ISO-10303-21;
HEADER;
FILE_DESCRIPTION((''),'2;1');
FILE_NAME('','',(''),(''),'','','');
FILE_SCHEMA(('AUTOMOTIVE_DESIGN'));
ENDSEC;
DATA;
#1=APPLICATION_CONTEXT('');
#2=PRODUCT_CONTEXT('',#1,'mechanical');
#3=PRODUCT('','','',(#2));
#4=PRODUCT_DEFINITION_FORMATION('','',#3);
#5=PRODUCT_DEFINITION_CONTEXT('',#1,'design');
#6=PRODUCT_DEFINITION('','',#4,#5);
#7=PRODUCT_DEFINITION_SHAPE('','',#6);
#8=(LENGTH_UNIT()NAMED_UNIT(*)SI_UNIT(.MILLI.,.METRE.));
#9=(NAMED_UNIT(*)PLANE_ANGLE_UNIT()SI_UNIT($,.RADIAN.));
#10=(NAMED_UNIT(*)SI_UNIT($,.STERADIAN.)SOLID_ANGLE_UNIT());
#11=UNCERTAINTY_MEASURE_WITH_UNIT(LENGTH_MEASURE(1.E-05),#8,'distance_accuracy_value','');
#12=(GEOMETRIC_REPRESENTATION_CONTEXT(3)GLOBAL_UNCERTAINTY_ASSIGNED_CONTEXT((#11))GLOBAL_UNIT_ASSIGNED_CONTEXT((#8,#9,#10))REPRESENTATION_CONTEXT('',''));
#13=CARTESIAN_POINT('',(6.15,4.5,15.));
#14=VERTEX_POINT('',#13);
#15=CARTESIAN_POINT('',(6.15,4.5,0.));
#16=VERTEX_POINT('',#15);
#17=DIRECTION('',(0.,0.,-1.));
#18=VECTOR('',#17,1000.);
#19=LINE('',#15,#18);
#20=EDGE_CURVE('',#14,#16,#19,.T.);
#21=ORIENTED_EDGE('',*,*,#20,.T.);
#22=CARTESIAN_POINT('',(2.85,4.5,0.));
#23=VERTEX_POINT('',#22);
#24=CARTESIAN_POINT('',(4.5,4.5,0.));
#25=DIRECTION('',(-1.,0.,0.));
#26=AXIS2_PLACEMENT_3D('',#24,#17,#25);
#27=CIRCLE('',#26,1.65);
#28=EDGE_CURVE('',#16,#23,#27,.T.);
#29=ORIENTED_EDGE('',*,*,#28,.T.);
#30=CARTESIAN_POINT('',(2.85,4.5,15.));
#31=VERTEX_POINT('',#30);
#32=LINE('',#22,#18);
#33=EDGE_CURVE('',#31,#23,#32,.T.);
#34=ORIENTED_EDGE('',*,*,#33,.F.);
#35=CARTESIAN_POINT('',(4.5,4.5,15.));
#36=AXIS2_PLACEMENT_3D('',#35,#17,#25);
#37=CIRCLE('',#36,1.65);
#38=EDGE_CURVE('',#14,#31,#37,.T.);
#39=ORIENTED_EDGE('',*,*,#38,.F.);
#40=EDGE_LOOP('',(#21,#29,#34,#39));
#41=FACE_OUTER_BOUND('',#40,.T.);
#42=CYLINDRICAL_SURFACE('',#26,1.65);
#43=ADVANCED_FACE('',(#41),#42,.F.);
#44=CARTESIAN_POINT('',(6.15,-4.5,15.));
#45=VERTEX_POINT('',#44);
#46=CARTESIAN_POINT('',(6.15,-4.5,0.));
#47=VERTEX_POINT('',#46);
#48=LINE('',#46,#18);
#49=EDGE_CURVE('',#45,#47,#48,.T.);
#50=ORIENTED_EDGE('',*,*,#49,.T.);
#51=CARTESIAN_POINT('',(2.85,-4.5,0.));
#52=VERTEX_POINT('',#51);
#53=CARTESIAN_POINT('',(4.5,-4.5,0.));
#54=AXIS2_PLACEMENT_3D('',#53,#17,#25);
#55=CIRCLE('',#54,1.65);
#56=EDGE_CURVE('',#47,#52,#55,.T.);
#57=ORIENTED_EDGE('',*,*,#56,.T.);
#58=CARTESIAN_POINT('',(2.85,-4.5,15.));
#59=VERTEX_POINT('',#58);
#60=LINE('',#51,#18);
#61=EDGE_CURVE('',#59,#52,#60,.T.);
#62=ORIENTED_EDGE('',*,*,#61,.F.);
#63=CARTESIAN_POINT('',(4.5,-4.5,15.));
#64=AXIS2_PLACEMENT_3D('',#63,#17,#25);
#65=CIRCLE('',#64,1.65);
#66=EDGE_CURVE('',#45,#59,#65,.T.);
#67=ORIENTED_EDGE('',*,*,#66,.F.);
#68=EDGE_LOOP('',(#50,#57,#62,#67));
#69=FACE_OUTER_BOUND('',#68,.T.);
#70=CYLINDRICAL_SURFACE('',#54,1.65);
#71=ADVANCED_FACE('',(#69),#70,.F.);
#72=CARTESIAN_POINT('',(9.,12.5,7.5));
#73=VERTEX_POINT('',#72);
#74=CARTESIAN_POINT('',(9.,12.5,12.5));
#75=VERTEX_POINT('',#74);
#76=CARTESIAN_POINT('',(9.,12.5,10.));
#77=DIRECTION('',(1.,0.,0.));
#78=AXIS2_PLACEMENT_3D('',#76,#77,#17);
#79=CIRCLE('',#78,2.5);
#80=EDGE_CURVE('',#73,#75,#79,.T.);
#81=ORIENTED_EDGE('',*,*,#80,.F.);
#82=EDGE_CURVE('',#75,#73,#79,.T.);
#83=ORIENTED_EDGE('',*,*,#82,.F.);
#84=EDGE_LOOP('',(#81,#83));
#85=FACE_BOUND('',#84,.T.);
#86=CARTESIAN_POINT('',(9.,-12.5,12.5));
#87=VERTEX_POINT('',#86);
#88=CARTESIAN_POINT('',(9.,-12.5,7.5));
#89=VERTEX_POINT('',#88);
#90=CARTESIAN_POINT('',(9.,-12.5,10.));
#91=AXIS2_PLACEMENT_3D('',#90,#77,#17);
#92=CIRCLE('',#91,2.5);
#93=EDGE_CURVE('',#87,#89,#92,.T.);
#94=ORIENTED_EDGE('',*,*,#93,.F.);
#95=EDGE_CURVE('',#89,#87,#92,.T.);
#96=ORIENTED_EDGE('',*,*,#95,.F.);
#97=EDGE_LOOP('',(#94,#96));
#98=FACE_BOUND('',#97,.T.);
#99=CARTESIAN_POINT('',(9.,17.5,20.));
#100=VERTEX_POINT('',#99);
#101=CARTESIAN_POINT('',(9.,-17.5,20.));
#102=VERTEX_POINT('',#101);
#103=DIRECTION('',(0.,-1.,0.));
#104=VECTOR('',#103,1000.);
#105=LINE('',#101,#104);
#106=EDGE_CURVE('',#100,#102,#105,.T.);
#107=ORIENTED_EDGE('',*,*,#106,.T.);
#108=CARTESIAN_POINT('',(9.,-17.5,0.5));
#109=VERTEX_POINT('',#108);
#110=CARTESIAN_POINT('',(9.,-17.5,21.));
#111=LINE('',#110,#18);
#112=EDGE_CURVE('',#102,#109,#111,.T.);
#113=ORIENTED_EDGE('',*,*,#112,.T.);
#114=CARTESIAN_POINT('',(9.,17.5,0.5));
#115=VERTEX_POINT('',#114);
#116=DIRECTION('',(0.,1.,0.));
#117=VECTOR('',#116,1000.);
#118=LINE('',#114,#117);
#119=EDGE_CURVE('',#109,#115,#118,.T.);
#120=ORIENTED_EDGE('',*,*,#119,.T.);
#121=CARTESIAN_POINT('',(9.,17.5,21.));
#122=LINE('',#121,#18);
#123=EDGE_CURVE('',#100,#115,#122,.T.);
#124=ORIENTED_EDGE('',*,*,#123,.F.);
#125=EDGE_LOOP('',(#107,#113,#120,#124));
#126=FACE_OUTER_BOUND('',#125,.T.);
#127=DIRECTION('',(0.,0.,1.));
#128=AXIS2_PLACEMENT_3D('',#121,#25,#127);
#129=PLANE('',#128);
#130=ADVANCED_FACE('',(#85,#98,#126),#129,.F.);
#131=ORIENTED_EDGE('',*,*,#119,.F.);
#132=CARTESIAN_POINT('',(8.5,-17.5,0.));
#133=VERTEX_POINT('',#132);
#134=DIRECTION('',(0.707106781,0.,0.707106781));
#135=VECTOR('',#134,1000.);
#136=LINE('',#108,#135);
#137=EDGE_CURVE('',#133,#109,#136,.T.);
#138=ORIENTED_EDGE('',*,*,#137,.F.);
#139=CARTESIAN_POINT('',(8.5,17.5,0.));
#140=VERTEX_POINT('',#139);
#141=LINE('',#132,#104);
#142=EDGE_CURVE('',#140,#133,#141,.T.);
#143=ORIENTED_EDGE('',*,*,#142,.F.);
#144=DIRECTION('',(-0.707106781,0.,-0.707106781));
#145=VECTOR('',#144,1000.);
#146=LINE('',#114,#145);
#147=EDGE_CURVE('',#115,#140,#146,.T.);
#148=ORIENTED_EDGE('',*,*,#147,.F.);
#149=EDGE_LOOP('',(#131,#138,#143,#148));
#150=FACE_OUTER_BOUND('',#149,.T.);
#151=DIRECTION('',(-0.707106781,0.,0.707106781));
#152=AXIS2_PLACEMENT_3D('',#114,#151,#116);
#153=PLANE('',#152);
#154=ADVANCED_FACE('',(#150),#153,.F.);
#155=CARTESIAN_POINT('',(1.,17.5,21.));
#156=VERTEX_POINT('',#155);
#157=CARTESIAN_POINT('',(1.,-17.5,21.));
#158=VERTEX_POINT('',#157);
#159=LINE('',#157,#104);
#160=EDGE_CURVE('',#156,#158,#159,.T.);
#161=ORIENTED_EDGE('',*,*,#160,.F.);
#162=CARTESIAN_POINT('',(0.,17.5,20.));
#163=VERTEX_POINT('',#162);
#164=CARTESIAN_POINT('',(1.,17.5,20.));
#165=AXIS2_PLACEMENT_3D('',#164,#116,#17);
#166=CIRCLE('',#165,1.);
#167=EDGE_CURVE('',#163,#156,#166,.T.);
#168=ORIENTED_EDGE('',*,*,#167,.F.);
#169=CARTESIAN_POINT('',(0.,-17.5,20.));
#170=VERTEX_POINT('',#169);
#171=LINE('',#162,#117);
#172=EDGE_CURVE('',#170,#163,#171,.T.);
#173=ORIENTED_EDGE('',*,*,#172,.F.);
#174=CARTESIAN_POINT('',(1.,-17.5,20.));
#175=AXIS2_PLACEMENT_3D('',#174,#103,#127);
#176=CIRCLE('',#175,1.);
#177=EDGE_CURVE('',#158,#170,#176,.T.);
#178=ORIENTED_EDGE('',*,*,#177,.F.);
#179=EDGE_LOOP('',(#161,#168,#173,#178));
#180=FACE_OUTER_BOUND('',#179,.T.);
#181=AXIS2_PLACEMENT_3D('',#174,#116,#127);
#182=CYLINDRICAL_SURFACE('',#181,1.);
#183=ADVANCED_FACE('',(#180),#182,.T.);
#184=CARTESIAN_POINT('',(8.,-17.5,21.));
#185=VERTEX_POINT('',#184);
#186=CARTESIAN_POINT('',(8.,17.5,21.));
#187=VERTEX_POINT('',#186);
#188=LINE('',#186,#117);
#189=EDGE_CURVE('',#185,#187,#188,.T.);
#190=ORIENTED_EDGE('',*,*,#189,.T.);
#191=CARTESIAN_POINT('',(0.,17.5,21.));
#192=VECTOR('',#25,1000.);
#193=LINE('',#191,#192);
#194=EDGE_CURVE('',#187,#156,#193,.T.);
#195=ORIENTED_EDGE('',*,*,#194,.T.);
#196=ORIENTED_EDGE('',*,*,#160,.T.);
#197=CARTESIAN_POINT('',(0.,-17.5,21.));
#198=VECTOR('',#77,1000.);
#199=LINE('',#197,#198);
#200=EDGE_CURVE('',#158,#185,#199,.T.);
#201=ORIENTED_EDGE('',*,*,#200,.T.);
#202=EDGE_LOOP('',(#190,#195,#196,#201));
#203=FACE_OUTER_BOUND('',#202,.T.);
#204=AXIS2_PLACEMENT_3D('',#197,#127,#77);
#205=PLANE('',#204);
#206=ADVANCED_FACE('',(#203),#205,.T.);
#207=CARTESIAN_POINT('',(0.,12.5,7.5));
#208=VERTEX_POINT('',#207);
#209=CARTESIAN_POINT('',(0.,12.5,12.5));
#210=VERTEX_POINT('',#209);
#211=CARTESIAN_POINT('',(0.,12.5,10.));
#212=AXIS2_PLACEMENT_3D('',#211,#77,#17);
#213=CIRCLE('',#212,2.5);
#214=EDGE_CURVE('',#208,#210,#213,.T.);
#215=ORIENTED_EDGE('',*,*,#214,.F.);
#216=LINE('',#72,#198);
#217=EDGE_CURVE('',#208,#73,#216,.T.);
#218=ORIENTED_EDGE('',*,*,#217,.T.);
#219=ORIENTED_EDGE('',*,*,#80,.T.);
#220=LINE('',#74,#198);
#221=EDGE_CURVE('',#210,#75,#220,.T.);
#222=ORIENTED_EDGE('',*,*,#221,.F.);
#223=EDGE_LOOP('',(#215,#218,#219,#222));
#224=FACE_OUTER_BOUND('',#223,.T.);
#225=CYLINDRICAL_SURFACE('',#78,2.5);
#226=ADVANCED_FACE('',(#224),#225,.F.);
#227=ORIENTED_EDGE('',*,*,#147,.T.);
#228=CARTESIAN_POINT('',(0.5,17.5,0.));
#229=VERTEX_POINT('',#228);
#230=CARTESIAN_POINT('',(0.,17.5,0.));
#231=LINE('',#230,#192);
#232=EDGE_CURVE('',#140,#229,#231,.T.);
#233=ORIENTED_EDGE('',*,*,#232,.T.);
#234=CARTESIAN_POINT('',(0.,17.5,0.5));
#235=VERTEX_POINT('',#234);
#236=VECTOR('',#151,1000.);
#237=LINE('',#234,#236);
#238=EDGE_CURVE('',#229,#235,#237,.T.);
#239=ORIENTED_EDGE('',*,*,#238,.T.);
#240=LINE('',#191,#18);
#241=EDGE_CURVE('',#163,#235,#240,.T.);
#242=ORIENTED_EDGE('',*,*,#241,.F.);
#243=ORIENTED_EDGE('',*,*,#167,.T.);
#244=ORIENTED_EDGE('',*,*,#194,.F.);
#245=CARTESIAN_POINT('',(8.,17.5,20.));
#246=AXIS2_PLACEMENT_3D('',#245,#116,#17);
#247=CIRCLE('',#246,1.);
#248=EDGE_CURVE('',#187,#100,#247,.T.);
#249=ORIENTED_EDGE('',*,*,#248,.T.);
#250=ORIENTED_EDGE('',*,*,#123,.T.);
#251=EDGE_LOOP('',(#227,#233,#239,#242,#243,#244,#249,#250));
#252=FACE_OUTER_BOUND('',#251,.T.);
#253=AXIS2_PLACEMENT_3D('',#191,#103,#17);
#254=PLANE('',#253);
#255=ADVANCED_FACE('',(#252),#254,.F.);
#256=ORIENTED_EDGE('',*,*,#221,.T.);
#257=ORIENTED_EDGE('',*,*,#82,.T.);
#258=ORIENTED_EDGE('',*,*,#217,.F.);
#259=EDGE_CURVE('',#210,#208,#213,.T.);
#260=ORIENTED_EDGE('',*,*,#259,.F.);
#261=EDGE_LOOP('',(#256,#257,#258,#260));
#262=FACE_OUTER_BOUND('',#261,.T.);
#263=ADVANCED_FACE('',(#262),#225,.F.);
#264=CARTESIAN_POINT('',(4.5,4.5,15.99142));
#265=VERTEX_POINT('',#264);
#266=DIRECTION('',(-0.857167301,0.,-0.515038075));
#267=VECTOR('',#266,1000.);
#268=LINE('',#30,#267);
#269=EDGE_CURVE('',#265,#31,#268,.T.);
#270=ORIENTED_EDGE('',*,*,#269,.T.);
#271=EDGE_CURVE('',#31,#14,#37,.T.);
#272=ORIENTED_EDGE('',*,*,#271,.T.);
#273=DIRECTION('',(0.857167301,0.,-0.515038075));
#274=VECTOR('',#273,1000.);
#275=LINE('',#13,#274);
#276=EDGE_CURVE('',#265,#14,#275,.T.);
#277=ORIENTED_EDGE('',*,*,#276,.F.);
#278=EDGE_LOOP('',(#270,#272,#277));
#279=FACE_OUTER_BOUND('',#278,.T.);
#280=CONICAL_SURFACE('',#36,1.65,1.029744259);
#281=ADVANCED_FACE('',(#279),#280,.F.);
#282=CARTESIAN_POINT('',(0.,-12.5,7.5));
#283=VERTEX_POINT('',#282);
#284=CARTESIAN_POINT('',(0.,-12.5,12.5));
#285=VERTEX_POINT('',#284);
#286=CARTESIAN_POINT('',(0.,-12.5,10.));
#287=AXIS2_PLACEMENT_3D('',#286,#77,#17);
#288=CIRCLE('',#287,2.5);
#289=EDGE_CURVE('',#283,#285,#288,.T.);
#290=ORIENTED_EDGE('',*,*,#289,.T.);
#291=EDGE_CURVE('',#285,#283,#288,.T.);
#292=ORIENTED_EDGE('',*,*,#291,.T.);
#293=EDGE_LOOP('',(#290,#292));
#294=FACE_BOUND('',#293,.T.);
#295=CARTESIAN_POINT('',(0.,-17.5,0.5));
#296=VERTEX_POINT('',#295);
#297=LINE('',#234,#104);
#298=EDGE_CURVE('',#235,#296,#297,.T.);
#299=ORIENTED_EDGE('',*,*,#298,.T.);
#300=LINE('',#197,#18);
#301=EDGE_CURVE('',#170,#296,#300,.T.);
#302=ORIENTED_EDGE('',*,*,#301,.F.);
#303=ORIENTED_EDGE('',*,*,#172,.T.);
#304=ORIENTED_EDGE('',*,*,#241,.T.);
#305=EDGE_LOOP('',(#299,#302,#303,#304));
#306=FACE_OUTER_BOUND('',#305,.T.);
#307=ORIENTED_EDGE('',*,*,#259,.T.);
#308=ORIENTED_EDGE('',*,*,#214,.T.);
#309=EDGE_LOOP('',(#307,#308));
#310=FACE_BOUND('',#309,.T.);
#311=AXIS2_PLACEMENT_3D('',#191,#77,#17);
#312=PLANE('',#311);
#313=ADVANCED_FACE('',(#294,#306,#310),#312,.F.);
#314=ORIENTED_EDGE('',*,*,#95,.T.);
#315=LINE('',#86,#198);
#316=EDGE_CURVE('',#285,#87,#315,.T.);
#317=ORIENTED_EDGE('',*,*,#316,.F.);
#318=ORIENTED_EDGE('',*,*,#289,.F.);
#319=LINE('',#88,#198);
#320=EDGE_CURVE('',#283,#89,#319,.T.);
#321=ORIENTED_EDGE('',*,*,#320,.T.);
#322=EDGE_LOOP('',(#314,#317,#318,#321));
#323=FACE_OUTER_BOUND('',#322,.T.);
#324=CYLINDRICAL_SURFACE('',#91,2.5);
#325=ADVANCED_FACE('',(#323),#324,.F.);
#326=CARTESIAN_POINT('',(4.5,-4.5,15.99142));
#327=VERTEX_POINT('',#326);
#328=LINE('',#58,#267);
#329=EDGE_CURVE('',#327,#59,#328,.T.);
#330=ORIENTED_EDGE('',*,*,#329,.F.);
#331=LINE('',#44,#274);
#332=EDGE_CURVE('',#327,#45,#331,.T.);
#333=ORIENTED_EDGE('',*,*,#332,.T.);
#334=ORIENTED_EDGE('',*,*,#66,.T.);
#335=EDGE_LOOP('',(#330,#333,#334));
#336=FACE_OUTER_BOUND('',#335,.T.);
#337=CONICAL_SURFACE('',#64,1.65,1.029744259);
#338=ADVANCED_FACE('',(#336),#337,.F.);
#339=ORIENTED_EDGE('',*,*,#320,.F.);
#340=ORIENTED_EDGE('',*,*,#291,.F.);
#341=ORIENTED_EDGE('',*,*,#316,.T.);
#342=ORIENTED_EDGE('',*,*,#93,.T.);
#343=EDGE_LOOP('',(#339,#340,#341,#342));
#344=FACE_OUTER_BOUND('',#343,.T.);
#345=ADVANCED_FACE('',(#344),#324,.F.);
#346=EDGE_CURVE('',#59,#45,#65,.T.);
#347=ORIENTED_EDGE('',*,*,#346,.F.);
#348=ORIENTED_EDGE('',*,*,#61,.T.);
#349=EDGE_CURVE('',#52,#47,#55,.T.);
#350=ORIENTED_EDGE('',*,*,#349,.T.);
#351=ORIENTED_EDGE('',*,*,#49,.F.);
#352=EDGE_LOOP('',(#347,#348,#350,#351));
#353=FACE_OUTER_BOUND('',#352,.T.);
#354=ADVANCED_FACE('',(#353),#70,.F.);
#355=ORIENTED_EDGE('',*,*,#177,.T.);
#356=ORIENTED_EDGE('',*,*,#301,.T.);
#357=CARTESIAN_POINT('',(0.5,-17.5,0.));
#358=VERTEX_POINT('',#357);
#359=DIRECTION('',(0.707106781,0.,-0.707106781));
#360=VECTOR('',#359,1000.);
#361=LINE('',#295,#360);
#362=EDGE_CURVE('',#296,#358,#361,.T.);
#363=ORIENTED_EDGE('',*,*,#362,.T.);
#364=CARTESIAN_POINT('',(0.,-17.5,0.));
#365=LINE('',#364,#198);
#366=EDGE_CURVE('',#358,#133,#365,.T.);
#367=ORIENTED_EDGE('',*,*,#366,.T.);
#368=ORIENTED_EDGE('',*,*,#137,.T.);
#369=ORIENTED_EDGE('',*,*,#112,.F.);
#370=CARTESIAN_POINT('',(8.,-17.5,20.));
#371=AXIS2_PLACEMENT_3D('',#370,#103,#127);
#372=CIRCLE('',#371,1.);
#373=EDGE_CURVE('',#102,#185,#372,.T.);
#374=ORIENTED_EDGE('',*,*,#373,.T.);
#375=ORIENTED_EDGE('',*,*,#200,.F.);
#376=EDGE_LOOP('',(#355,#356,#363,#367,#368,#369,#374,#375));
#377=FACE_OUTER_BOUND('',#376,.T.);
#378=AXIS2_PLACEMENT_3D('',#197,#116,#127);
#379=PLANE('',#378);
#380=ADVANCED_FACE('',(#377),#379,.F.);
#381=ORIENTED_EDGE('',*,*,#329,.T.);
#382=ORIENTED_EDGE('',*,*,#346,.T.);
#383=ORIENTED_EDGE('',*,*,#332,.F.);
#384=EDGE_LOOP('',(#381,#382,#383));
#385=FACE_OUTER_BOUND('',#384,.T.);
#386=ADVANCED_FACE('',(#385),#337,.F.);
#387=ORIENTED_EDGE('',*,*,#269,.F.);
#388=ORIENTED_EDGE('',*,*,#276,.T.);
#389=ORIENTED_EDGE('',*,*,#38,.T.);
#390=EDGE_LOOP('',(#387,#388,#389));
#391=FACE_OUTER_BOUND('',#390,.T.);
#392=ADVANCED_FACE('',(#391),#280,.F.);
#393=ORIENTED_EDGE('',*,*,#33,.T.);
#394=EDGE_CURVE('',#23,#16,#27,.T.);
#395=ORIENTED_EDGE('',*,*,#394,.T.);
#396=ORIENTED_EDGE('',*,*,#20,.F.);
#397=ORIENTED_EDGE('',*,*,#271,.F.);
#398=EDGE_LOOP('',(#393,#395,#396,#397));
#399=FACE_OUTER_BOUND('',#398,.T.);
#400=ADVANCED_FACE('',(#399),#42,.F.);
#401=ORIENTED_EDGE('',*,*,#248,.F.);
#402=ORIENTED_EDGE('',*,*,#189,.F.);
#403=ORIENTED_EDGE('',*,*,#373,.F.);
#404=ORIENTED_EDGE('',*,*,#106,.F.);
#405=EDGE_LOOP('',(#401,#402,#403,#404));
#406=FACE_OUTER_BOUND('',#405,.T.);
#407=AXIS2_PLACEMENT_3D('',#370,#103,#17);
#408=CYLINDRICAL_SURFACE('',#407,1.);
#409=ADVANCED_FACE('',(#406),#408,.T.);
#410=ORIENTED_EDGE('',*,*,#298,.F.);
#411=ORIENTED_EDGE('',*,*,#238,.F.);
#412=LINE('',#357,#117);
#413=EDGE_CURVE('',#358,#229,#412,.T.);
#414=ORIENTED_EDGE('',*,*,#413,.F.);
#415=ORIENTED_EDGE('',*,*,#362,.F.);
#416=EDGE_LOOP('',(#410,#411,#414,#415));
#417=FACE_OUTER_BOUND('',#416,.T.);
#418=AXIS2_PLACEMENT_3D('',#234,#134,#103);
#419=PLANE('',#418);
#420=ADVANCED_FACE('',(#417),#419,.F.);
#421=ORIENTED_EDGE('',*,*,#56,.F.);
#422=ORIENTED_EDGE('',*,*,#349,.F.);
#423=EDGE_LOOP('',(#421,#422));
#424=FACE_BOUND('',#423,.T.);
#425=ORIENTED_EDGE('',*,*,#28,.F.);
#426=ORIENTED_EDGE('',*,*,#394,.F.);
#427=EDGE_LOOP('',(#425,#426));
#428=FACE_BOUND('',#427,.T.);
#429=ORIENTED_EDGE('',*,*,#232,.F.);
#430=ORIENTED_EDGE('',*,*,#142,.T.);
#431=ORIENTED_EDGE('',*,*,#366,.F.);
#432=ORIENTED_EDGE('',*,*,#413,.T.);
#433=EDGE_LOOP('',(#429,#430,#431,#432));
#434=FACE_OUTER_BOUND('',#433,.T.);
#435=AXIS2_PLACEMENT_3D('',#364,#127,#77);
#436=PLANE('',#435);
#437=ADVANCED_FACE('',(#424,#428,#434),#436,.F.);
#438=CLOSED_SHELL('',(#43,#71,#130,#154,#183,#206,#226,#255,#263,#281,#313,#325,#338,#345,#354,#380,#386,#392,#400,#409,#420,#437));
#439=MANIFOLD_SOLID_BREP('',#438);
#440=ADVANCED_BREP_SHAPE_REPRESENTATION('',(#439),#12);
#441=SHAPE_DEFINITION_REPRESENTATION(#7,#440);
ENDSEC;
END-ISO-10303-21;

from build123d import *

# Parameters (mm, degrees)
SKETCH1_W             = 9
SKETCH1_H             = 35
BOSS_EXTRUDE1_DEPTH   = 21
M6_TAPPED_HOLE1_D     = 5
M6_TAPPED_HOLE1_DEPTH = 15
M6_TAPPED_HOLE1_TIP   = 1.502151548
M4_TAPPED_HOLE1_D     = 3.3
M4_TAPPED_HOLE1_DEPTH = 15
M4_TAPPED_HOLE1_TIP   = 0.991420021
FILLET1_R             = 1
CHAMFER1_SIZE         = 0.5


with BuildPart() as part:
    # Sketch1 → Boss-Extrude1 (new body)
    with BuildSketch(Plane.XY):
        with Locations((4.5, 0)):
            Rectangle(SKETCH1_W, SKETCH1_H)
    extrude(amount=BOSS_EXTRUDE1_DEPTH)

    # M6 Tapped Hole1
    with Locations(Plane(origin=(9, 0, 0), x_dir=(0, 0, -1), z_dir=(1, 0, 0))):
        with Locations((-10, 12.5), (-10, -12.5)):
            Hole(M6_TAPPED_HOLE1_D / 2, depth=M6_TAPPED_HOLE1_DEPTH)
            with Locations((0, 0, -(M6_TAPPED_HOLE1_DEPTH + M6_TAPPED_HOLE1_TIP / 2))):  # 118° drill point
                Cone(0, M6_TAPPED_HOLE1_D / 2, M6_TAPPED_HOLE1_TIP, mode=Mode.SUBTRACT)

    # M4 Tapped Hole1
    with Locations(Plane(origin=(0, 0, 0), x_dir=(-1, 0, 0), z_dir=(0, 0, -1))):
        with Locations((-4.5, 4.5), (-4.5, -4.5)):
            Hole(M4_TAPPED_HOLE1_D / 2, depth=M4_TAPPED_HOLE1_DEPTH)
            with Locations((0, 0, -(M4_TAPPED_HOLE1_DEPTH + M4_TAPPED_HOLE1_TIP / 2))):  # 118° drill point
                Cone(0, M4_TAPPED_HOLE1_D / 2, M4_TAPPED_HOLE1_TIP, mode=Mode.SUBTRACT)

    # Fillet1
    fillet1_edges = [part.edges().sort_by_distance(p)[0] for p in [
        (9, 0, 21),
        (0, 0, 21),
    ]]
    fillet(fillet1_edges, radius=FILLET1_R)

    # Chamfer1
    chamfer1_edges = [part.edges().sort_by_distance(p)[0] for p in [
        (9, 0, 0),
        (0, 0, 0),
    ]]
    chamfer(chamfer1_edges, length=CHAMFER1_SIZE)


solid = part.part
